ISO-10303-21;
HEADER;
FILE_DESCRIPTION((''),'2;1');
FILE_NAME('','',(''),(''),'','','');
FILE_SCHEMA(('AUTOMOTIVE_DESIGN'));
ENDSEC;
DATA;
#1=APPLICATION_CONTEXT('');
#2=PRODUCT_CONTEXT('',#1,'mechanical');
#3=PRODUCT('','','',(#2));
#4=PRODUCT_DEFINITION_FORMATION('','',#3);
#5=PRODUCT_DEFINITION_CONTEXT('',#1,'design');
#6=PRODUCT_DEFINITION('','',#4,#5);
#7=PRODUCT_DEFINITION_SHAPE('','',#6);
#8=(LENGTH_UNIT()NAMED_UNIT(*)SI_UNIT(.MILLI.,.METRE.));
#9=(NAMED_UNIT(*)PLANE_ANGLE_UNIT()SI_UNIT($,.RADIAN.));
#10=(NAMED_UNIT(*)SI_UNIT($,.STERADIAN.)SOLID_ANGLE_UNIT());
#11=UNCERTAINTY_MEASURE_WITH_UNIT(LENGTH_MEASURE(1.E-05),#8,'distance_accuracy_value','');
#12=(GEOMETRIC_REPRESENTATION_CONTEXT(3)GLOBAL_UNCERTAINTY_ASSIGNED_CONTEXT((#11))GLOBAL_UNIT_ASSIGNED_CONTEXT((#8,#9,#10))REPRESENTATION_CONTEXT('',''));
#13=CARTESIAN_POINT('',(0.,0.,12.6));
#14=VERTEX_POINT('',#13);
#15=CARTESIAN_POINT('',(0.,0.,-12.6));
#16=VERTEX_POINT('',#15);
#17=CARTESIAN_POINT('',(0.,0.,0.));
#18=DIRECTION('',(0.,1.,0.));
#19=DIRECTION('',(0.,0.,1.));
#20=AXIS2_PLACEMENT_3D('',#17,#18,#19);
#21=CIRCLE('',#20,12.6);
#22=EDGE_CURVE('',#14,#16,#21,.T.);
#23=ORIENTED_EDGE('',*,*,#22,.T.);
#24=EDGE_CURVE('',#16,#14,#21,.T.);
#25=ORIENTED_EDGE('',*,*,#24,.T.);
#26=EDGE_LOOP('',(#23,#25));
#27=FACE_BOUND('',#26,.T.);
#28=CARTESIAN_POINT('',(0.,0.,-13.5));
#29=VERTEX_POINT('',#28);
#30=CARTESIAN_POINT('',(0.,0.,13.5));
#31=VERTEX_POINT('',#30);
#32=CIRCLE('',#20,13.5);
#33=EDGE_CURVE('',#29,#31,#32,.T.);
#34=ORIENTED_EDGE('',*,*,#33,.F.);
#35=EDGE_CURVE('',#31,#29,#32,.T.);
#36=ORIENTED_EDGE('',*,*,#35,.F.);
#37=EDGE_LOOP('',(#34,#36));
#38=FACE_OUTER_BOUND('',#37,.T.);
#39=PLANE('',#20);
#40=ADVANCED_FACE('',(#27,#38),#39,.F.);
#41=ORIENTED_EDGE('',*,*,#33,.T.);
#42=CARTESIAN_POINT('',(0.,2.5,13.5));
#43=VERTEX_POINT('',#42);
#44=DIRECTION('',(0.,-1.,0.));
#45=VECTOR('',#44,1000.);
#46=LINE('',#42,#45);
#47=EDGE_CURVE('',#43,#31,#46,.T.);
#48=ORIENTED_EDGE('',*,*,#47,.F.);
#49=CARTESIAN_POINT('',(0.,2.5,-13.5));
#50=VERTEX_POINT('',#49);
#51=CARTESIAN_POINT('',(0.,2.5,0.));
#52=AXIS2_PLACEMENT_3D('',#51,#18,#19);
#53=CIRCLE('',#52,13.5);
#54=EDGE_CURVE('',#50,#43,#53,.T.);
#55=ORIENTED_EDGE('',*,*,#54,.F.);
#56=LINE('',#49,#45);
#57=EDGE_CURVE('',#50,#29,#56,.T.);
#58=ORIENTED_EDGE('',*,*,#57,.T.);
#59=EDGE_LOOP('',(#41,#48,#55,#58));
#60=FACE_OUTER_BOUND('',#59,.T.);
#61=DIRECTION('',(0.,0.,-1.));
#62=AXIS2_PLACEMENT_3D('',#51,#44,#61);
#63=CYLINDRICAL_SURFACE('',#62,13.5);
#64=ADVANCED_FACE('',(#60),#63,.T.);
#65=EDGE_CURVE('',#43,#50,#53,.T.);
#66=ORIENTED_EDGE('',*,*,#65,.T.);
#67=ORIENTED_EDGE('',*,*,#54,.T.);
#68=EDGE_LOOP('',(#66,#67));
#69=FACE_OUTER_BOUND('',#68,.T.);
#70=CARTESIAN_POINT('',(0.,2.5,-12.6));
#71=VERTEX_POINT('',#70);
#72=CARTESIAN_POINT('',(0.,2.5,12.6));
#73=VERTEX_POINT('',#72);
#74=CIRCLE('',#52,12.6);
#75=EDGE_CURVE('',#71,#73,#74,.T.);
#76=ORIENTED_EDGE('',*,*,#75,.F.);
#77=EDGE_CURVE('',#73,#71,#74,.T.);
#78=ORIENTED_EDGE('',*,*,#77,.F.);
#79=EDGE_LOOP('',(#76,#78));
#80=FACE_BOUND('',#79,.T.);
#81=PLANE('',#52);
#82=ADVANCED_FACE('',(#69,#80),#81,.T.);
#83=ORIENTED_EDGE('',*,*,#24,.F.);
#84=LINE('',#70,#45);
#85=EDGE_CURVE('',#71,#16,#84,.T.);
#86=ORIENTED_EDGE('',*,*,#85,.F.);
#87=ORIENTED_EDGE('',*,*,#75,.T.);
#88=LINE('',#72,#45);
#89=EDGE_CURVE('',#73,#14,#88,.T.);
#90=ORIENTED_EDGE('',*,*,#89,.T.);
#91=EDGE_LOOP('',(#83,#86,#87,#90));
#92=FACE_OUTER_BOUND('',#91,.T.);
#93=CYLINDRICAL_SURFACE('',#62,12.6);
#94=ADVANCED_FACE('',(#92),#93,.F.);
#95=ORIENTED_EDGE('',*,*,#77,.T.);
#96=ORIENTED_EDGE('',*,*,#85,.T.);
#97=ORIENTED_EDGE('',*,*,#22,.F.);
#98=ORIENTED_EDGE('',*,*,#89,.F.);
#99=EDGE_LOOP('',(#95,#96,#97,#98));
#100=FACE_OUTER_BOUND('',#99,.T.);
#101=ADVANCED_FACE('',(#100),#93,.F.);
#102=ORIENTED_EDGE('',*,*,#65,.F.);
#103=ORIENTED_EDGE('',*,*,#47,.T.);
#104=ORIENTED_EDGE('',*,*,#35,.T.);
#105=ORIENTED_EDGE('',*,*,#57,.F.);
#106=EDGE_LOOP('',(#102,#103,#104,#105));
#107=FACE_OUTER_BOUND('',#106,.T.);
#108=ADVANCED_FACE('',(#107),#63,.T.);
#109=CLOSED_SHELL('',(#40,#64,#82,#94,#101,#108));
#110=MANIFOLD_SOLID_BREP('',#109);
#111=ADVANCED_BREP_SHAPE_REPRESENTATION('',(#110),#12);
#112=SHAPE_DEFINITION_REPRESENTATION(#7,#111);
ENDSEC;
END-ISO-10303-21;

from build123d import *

# Parameters (mm, degrees)
SKETCH1_R           = 13.5
SKETCH1_R_2         = 12.6
BOSS_EXTRUDE1_DEPTH = 2.5


with BuildPart() as part:
    # Sketch1 → Boss-Extrude1 (new body)
    with BuildSketch(Plane(origin=(0, 0, 0), x_dir=(1, 0, 0), z_dir=(0, 1, 0))):
        with Locations(Location((0, 0, 0), (0, 0, 270))):
            Circle(SKETCH1_R)
        with Locations(Location((0, 0, 0), (0, 0, 270))):
            Circle(SKETCH1_R_2, mode=Mode.SUBTRACT)
    extrude(amount=BOSS_EXTRUDE1_DEPTH)


solid = part.part
